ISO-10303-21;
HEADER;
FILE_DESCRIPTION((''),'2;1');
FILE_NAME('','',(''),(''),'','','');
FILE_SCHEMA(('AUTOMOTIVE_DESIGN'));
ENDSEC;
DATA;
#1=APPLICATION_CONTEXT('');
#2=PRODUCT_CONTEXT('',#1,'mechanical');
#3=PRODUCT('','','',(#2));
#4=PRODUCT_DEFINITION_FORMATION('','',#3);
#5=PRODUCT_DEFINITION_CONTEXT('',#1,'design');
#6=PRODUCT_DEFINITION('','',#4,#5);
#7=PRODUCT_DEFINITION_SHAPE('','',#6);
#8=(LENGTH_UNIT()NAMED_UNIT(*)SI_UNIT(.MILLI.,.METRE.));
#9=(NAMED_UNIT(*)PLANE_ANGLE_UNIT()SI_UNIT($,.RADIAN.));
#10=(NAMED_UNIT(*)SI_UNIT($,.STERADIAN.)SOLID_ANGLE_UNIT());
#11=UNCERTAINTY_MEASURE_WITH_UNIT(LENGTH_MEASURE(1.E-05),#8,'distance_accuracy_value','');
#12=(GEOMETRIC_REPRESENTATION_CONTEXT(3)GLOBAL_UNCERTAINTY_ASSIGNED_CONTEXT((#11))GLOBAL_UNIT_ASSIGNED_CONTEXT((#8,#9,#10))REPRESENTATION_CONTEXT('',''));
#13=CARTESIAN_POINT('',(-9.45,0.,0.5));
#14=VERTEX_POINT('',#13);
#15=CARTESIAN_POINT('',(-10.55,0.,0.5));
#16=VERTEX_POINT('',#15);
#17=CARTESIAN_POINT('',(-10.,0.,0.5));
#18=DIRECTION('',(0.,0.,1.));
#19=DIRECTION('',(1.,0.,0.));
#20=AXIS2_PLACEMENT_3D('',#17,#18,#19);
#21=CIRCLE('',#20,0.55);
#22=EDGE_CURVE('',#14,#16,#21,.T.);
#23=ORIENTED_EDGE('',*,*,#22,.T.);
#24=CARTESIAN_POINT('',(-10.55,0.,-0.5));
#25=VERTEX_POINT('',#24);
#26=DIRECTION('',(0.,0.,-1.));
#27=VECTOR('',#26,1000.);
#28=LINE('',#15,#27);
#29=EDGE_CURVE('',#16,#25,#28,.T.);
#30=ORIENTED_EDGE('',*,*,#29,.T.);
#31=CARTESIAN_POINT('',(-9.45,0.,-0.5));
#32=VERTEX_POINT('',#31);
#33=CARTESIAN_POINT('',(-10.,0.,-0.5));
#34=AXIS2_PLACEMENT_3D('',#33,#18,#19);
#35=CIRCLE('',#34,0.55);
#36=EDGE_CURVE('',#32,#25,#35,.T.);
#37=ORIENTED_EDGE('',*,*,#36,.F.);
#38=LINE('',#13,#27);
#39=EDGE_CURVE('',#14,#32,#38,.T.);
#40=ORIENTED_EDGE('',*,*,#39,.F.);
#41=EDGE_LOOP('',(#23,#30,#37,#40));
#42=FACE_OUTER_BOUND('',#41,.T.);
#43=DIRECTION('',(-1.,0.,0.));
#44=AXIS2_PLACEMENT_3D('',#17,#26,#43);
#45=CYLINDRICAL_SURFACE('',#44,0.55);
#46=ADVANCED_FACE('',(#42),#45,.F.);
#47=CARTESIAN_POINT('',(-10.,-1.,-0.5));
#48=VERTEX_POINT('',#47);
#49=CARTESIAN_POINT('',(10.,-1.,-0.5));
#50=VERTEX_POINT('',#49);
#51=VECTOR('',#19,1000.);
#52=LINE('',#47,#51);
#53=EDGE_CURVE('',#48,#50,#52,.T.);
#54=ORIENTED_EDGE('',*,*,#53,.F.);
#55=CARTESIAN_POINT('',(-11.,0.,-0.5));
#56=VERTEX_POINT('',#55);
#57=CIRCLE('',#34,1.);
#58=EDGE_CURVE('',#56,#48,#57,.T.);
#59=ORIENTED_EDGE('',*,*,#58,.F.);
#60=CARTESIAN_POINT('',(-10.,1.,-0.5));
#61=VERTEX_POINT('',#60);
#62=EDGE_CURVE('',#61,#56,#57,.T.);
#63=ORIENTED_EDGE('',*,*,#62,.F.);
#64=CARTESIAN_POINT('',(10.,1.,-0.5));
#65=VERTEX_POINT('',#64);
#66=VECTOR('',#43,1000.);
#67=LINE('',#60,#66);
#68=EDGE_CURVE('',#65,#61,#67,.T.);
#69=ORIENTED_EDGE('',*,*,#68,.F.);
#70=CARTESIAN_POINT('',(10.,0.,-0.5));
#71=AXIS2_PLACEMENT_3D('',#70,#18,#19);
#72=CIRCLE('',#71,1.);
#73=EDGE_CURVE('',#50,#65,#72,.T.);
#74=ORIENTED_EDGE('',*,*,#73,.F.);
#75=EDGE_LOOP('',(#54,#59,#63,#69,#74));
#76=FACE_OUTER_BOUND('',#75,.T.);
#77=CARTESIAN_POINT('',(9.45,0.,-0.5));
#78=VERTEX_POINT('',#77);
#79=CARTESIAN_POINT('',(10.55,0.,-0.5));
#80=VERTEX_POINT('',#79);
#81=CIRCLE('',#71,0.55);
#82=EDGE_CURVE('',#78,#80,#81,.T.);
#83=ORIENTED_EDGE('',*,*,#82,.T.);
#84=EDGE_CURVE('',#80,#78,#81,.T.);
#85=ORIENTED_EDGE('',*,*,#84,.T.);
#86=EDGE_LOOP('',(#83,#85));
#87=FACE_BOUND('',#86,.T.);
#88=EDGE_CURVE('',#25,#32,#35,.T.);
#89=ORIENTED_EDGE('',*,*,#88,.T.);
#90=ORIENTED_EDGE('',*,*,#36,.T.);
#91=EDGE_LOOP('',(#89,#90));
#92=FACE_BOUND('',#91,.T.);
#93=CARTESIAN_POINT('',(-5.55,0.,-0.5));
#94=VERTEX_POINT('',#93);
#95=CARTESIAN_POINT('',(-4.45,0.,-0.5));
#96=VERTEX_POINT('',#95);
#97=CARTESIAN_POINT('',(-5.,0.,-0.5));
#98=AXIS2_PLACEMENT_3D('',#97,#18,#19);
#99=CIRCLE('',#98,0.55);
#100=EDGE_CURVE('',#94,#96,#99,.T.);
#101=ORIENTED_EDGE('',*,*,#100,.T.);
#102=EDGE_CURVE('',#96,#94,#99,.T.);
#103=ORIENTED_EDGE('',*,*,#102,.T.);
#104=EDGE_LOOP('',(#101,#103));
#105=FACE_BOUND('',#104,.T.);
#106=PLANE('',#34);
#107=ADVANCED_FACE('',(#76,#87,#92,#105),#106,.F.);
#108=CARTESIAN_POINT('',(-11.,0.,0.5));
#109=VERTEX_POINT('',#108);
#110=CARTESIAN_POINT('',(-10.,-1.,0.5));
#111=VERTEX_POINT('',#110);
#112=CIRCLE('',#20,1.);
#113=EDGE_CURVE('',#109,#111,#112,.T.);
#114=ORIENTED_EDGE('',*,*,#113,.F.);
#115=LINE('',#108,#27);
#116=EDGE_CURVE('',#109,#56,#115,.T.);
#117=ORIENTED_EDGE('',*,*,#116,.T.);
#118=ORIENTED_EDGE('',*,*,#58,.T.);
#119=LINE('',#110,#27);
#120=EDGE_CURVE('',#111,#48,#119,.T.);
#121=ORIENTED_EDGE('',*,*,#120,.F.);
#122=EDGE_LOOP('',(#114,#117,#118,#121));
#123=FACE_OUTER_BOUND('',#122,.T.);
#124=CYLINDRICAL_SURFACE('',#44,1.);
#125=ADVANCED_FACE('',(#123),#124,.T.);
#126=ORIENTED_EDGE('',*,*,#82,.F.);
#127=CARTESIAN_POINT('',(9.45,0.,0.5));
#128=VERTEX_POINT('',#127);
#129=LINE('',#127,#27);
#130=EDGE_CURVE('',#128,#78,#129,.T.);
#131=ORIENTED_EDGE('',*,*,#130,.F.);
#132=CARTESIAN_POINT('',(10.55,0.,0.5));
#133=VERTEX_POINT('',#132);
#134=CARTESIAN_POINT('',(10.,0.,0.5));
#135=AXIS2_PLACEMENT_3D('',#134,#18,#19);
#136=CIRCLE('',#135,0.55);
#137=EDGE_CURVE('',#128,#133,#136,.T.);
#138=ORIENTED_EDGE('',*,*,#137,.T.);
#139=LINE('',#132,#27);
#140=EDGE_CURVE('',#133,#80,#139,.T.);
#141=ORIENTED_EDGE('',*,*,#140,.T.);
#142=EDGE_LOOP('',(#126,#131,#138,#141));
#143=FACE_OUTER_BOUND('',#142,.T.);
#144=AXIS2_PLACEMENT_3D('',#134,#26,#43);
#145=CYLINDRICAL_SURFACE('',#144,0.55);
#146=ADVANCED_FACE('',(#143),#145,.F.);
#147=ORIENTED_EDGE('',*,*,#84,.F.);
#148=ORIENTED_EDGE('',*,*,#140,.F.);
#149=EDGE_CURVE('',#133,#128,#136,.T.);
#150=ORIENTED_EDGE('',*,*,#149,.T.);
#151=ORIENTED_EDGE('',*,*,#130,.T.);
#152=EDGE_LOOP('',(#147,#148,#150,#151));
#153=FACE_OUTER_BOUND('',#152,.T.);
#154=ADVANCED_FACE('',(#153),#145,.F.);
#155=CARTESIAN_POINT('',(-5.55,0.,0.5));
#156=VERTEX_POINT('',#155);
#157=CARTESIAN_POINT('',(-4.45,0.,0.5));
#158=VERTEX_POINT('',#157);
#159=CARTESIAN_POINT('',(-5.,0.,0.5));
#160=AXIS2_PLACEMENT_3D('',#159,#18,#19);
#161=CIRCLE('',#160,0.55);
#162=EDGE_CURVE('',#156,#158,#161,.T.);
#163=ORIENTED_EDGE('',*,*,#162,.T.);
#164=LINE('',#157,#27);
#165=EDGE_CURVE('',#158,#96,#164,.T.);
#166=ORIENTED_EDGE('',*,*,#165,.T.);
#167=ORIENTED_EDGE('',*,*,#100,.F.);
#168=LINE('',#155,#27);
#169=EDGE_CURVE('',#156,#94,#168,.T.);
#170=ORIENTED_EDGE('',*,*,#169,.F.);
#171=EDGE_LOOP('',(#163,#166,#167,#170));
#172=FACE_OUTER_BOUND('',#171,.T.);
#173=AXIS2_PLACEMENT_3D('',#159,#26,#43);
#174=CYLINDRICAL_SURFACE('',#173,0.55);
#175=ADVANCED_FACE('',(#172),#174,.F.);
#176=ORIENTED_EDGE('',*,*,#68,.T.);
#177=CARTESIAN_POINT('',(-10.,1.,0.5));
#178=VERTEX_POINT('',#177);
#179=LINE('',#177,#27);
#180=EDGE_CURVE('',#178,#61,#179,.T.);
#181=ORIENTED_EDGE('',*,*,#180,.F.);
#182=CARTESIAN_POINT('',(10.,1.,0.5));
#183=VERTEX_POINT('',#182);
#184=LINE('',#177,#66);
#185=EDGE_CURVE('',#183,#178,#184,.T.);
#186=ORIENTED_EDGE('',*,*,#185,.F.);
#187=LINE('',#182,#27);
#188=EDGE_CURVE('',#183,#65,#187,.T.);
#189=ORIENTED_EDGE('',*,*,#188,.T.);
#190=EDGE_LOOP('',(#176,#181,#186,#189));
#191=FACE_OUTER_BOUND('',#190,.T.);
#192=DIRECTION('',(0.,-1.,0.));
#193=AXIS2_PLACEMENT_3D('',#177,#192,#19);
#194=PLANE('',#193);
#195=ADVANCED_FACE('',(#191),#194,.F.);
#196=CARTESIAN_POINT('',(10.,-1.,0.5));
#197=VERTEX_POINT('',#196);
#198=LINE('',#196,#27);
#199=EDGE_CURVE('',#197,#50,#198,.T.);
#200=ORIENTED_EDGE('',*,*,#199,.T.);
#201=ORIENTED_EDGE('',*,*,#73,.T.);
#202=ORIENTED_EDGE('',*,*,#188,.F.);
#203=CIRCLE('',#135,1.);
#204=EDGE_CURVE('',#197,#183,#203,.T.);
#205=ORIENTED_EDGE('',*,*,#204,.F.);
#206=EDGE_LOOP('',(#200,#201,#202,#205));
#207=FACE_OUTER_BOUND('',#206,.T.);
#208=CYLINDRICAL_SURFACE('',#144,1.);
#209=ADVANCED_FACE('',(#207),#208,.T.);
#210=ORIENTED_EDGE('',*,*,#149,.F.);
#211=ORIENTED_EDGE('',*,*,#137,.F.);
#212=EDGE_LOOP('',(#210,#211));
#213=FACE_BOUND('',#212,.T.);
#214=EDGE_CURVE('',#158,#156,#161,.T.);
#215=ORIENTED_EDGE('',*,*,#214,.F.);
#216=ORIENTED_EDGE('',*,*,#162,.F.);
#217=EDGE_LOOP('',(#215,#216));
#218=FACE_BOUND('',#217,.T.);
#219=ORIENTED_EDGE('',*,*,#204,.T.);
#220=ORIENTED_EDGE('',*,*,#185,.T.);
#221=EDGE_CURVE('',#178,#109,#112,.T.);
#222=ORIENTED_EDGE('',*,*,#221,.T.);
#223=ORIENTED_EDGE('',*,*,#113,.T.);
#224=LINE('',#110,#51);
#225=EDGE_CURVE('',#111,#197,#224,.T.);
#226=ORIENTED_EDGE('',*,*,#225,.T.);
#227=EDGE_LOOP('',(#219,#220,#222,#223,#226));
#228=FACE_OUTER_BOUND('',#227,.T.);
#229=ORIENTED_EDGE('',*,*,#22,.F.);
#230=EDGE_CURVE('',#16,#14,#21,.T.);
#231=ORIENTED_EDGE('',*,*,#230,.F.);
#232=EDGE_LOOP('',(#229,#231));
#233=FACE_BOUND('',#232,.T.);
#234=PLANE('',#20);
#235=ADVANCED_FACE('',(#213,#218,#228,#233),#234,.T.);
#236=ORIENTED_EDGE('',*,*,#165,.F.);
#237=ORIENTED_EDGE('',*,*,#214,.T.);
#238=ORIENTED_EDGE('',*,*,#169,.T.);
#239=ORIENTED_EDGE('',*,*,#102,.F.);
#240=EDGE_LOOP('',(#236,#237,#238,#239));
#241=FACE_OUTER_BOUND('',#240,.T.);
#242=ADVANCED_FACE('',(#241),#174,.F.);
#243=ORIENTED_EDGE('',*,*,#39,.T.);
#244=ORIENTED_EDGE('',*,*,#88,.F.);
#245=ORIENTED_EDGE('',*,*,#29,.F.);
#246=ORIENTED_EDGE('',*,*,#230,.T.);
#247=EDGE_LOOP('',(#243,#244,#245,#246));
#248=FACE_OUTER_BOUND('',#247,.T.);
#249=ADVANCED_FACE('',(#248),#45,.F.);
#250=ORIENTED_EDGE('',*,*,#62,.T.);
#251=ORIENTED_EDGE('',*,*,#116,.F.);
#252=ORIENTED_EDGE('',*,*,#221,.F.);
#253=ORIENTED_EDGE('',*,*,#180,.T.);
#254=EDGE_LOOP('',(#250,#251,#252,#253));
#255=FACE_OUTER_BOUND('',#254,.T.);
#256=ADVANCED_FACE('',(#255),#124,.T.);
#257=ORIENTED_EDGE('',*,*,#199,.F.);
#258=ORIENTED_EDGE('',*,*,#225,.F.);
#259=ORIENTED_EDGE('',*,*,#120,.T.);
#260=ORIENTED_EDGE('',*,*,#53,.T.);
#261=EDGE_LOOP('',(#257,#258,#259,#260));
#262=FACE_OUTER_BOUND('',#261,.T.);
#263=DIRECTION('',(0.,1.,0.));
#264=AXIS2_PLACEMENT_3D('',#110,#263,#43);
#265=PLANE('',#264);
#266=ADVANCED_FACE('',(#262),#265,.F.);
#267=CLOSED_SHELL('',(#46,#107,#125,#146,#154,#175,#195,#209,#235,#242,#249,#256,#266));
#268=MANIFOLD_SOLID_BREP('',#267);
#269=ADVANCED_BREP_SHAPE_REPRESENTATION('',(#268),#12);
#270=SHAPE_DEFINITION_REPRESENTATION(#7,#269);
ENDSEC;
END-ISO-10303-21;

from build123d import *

# Parameters (mm, degrees)
SKETCH1_R           = 0.55
THIGH1_LENGTH_DEPTH = 0.5


with BuildPart() as part:
    # Sketch1 → Thigh1 length (new, symmetric)
    with BuildSketch(Plane.XY):
        with BuildLine():
            Line((-10, 1), (10, 1))
            ThreePointArc((10, 1), (11, 0), (10, -1))
            Line((10, -1), (-10, -1))
            ThreePointArc((-10, -1), (-11, 0), (-10, 1))
        make_face()
        with Locations((-10, 0)):
            Circle(SKETCH1_R, mode=Mode.SUBTRACT)
        with Locations((10, 0)):
            Circle(SKETCH1_R, mode=Mode.SUBTRACT)
        with Locations((-5, 0)):
            Circle(SKETCH1_R, mode=Mode.SUBTRACT)
    extrude(amount=THIGH1_LENGTH_DEPTH, both=True)


solid = part.part
